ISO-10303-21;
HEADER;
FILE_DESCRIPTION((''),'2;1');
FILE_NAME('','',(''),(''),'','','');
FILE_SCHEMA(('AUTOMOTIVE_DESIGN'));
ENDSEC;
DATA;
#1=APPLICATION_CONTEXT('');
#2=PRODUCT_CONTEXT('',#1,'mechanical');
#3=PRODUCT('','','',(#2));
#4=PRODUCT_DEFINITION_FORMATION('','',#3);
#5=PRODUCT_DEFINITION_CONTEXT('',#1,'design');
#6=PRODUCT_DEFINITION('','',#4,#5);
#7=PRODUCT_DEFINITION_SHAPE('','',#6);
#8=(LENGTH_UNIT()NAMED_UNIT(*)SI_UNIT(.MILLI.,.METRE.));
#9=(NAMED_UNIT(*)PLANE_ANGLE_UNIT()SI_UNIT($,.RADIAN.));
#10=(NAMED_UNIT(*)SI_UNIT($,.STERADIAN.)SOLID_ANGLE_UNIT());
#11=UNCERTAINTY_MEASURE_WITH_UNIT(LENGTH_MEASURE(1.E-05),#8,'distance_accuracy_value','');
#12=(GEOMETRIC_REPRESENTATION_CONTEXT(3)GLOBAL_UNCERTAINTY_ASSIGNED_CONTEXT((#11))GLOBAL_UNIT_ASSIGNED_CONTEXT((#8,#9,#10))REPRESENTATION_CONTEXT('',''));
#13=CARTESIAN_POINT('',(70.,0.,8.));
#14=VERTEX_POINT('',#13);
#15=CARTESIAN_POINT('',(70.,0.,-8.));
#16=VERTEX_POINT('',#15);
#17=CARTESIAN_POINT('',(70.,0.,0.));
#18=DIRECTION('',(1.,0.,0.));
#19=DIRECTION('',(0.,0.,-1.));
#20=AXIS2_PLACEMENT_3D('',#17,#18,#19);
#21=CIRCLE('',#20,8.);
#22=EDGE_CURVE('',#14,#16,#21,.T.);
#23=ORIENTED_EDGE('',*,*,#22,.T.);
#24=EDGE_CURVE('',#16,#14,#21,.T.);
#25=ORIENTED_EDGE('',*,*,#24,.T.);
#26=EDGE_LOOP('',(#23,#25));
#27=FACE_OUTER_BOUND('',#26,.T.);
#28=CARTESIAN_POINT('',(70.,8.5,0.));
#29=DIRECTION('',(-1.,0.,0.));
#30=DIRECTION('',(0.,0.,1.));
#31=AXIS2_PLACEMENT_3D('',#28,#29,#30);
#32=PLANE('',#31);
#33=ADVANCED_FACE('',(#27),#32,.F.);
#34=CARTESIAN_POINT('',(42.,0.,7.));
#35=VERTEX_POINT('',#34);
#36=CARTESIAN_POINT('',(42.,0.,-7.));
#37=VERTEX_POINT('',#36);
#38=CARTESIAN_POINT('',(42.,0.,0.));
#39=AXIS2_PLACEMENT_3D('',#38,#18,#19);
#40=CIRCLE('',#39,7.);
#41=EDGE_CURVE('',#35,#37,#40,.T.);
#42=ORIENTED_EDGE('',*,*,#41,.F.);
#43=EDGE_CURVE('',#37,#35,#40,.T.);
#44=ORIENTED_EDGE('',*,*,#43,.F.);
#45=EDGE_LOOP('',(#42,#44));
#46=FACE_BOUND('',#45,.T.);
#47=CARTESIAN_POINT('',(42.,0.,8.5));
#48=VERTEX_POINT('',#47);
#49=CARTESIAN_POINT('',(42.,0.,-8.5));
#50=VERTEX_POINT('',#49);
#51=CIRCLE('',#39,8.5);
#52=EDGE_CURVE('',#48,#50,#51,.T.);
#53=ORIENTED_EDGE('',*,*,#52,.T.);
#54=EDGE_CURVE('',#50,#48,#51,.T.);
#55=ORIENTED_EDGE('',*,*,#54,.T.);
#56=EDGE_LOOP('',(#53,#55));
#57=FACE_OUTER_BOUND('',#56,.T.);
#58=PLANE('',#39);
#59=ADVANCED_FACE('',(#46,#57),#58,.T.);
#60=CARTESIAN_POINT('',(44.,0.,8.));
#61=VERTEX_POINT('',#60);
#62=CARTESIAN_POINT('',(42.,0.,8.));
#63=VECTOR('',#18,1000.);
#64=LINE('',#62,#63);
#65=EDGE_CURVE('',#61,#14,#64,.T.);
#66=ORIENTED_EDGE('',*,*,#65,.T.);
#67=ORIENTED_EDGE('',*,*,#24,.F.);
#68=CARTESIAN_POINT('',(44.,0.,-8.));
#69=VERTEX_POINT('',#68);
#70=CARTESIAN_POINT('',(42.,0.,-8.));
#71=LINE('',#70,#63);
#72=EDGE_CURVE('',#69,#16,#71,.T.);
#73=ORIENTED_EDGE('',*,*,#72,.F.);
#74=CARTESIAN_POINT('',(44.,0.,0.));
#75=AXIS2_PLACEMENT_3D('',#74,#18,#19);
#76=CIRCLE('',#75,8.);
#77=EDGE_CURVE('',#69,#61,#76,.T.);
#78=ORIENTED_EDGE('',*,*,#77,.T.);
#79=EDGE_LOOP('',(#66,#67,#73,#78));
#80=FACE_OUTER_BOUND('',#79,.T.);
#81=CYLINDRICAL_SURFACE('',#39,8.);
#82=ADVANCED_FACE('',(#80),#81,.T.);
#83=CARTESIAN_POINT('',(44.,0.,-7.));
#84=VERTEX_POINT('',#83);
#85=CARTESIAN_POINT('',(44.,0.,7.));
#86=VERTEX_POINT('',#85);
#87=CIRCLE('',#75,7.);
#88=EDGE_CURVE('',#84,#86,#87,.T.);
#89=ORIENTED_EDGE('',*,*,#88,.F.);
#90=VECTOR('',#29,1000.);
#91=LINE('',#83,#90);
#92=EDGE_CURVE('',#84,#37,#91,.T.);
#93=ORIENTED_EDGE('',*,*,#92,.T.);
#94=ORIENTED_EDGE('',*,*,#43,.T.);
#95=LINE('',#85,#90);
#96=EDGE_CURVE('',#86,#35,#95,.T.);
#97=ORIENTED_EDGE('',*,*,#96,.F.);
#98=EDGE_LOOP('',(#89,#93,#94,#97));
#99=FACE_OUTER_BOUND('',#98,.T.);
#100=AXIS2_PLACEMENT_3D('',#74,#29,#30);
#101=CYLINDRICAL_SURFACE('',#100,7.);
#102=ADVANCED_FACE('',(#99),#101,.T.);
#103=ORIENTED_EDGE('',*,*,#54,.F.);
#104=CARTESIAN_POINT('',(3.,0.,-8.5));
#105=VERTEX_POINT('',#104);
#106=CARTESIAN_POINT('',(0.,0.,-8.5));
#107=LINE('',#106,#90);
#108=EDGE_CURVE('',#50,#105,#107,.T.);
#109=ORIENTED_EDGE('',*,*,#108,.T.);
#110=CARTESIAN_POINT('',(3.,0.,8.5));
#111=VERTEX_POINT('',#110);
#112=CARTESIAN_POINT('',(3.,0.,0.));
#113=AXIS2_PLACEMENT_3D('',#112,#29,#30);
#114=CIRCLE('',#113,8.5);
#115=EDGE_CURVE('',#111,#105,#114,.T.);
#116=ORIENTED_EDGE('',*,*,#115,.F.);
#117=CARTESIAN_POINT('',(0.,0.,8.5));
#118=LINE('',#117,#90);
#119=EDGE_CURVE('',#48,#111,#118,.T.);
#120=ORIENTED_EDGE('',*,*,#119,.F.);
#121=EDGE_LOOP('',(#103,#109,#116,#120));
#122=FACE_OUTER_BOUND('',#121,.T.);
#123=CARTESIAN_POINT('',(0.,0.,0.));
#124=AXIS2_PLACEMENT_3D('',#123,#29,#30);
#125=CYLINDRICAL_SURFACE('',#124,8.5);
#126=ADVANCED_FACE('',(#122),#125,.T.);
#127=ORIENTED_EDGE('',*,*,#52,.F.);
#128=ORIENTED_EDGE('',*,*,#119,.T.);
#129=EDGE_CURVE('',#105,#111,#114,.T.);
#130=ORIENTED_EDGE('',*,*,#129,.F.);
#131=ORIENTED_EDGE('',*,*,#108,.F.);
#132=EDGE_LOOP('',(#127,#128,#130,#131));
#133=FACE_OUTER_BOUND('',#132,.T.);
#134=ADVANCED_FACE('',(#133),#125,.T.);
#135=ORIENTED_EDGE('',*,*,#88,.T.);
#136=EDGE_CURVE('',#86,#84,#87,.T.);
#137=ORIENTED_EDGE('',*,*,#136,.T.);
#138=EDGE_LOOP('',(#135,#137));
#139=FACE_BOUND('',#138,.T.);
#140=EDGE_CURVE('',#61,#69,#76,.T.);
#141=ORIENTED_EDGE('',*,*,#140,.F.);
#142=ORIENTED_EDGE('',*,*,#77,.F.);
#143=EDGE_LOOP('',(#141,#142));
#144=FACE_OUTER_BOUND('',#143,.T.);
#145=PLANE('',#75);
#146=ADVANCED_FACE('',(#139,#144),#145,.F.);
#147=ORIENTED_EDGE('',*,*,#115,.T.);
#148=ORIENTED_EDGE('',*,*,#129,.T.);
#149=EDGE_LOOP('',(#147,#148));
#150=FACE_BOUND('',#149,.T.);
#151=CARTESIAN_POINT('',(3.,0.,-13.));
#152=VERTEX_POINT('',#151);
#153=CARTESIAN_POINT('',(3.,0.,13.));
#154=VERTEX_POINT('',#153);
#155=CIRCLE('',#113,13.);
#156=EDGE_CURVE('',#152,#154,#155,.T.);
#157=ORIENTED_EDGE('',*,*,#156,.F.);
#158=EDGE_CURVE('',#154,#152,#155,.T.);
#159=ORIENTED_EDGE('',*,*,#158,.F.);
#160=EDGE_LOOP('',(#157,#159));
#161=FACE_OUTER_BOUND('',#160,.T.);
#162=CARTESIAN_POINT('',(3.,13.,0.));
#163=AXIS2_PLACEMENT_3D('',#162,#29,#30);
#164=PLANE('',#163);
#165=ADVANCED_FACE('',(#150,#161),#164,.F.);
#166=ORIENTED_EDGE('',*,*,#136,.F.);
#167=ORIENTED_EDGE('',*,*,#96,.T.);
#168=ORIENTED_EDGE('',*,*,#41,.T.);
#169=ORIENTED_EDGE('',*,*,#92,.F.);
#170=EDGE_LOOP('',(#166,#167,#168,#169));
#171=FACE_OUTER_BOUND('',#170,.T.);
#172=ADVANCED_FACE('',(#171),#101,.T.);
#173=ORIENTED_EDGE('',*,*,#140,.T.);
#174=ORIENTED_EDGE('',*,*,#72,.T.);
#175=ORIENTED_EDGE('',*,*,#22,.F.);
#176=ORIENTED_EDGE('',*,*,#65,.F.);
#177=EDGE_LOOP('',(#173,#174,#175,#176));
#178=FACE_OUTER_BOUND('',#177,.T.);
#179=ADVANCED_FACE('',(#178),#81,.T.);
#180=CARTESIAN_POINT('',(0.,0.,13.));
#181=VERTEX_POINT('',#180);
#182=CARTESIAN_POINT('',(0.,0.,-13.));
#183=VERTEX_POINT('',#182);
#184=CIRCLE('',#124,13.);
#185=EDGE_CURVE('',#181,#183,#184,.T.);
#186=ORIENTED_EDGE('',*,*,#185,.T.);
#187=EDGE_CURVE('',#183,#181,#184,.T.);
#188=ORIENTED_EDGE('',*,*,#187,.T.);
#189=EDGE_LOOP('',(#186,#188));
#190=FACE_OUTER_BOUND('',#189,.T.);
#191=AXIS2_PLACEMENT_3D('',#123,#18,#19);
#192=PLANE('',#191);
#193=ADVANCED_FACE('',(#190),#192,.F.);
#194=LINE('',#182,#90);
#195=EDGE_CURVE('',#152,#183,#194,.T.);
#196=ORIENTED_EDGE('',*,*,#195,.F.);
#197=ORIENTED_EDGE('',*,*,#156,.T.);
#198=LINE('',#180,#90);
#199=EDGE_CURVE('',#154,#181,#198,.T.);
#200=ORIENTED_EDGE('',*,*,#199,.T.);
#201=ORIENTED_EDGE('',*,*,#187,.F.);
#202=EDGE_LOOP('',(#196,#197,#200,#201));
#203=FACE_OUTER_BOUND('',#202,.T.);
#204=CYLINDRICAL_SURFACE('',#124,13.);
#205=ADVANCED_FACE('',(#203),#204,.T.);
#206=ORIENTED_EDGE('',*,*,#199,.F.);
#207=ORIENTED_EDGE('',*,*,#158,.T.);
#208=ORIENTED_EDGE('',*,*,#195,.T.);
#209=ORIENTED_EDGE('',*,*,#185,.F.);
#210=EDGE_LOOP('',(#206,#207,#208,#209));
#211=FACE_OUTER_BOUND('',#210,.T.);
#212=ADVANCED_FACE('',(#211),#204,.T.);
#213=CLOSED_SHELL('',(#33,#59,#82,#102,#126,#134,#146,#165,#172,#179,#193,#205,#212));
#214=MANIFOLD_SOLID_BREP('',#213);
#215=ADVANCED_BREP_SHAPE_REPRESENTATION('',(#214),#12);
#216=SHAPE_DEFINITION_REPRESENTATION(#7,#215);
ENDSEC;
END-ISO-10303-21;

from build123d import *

# Parameters (mm, degrees)
SKETCH_2_R          = 8.5
SKETCH_2_R_2        = 8
CUT_EXTRUDE_1_DEPTH = 28
CUT_EXTRUDE_START   = 2
SKETCH_3_R          = 8
SKETCH_3_R_2        = 7
CUT_EXTRUDE_2_DEPTH = 2


with BuildPart() as part:
    # 草图1 → 旋转1 (revolve)
    with BuildSketch(Plane.XY, mode=Mode.PRIVATE) as revolve_1_sk:
        Polygon((0, 0), (0, 13), (3, 13), (3, 8.5), (70, 8.5), (70, 0), align=None)
    revolve(revolve_1_sk.sketch.rotate(Axis((0, 0, 0), (1, 0, 0)), 90), axis=Axis((0, 0, 0), (1, 0, 0)))

    # 草图2 → 切除-拉伸1 (cut)
    with BuildSketch(Plane(origin=(70, 0, 0), x_dir=(0, 0, -1), z_dir=(1, 0, 0))):
        with Locations(Location((0, 0, 0), (0, 0, 180))):
            Circle(SKETCH_2_R)
        Circle(SKETCH_2_R_2, mode=Mode.SUBTRACT)
    extrude(amount=-CUT_EXTRUDE_1_DEPTH, mode=Mode.SUBTRACT)

    # 草图3 → 切除-拉伸2 (cut)
    with BuildSketch(Plane(origin=(42, 0, 0), x_dir=(0, 0, -1), z_dir=(1, 0, 0)).offset(CUT_EXTRUDE_START)):
        Circle(SKETCH_3_R)
        Circle(SKETCH_3_R_2, mode=Mode.SUBTRACT)
    extrude(amount=-CUT_EXTRUDE_2_DEPTH, mode=Mode.SUBTRACT)


solid = part.part
